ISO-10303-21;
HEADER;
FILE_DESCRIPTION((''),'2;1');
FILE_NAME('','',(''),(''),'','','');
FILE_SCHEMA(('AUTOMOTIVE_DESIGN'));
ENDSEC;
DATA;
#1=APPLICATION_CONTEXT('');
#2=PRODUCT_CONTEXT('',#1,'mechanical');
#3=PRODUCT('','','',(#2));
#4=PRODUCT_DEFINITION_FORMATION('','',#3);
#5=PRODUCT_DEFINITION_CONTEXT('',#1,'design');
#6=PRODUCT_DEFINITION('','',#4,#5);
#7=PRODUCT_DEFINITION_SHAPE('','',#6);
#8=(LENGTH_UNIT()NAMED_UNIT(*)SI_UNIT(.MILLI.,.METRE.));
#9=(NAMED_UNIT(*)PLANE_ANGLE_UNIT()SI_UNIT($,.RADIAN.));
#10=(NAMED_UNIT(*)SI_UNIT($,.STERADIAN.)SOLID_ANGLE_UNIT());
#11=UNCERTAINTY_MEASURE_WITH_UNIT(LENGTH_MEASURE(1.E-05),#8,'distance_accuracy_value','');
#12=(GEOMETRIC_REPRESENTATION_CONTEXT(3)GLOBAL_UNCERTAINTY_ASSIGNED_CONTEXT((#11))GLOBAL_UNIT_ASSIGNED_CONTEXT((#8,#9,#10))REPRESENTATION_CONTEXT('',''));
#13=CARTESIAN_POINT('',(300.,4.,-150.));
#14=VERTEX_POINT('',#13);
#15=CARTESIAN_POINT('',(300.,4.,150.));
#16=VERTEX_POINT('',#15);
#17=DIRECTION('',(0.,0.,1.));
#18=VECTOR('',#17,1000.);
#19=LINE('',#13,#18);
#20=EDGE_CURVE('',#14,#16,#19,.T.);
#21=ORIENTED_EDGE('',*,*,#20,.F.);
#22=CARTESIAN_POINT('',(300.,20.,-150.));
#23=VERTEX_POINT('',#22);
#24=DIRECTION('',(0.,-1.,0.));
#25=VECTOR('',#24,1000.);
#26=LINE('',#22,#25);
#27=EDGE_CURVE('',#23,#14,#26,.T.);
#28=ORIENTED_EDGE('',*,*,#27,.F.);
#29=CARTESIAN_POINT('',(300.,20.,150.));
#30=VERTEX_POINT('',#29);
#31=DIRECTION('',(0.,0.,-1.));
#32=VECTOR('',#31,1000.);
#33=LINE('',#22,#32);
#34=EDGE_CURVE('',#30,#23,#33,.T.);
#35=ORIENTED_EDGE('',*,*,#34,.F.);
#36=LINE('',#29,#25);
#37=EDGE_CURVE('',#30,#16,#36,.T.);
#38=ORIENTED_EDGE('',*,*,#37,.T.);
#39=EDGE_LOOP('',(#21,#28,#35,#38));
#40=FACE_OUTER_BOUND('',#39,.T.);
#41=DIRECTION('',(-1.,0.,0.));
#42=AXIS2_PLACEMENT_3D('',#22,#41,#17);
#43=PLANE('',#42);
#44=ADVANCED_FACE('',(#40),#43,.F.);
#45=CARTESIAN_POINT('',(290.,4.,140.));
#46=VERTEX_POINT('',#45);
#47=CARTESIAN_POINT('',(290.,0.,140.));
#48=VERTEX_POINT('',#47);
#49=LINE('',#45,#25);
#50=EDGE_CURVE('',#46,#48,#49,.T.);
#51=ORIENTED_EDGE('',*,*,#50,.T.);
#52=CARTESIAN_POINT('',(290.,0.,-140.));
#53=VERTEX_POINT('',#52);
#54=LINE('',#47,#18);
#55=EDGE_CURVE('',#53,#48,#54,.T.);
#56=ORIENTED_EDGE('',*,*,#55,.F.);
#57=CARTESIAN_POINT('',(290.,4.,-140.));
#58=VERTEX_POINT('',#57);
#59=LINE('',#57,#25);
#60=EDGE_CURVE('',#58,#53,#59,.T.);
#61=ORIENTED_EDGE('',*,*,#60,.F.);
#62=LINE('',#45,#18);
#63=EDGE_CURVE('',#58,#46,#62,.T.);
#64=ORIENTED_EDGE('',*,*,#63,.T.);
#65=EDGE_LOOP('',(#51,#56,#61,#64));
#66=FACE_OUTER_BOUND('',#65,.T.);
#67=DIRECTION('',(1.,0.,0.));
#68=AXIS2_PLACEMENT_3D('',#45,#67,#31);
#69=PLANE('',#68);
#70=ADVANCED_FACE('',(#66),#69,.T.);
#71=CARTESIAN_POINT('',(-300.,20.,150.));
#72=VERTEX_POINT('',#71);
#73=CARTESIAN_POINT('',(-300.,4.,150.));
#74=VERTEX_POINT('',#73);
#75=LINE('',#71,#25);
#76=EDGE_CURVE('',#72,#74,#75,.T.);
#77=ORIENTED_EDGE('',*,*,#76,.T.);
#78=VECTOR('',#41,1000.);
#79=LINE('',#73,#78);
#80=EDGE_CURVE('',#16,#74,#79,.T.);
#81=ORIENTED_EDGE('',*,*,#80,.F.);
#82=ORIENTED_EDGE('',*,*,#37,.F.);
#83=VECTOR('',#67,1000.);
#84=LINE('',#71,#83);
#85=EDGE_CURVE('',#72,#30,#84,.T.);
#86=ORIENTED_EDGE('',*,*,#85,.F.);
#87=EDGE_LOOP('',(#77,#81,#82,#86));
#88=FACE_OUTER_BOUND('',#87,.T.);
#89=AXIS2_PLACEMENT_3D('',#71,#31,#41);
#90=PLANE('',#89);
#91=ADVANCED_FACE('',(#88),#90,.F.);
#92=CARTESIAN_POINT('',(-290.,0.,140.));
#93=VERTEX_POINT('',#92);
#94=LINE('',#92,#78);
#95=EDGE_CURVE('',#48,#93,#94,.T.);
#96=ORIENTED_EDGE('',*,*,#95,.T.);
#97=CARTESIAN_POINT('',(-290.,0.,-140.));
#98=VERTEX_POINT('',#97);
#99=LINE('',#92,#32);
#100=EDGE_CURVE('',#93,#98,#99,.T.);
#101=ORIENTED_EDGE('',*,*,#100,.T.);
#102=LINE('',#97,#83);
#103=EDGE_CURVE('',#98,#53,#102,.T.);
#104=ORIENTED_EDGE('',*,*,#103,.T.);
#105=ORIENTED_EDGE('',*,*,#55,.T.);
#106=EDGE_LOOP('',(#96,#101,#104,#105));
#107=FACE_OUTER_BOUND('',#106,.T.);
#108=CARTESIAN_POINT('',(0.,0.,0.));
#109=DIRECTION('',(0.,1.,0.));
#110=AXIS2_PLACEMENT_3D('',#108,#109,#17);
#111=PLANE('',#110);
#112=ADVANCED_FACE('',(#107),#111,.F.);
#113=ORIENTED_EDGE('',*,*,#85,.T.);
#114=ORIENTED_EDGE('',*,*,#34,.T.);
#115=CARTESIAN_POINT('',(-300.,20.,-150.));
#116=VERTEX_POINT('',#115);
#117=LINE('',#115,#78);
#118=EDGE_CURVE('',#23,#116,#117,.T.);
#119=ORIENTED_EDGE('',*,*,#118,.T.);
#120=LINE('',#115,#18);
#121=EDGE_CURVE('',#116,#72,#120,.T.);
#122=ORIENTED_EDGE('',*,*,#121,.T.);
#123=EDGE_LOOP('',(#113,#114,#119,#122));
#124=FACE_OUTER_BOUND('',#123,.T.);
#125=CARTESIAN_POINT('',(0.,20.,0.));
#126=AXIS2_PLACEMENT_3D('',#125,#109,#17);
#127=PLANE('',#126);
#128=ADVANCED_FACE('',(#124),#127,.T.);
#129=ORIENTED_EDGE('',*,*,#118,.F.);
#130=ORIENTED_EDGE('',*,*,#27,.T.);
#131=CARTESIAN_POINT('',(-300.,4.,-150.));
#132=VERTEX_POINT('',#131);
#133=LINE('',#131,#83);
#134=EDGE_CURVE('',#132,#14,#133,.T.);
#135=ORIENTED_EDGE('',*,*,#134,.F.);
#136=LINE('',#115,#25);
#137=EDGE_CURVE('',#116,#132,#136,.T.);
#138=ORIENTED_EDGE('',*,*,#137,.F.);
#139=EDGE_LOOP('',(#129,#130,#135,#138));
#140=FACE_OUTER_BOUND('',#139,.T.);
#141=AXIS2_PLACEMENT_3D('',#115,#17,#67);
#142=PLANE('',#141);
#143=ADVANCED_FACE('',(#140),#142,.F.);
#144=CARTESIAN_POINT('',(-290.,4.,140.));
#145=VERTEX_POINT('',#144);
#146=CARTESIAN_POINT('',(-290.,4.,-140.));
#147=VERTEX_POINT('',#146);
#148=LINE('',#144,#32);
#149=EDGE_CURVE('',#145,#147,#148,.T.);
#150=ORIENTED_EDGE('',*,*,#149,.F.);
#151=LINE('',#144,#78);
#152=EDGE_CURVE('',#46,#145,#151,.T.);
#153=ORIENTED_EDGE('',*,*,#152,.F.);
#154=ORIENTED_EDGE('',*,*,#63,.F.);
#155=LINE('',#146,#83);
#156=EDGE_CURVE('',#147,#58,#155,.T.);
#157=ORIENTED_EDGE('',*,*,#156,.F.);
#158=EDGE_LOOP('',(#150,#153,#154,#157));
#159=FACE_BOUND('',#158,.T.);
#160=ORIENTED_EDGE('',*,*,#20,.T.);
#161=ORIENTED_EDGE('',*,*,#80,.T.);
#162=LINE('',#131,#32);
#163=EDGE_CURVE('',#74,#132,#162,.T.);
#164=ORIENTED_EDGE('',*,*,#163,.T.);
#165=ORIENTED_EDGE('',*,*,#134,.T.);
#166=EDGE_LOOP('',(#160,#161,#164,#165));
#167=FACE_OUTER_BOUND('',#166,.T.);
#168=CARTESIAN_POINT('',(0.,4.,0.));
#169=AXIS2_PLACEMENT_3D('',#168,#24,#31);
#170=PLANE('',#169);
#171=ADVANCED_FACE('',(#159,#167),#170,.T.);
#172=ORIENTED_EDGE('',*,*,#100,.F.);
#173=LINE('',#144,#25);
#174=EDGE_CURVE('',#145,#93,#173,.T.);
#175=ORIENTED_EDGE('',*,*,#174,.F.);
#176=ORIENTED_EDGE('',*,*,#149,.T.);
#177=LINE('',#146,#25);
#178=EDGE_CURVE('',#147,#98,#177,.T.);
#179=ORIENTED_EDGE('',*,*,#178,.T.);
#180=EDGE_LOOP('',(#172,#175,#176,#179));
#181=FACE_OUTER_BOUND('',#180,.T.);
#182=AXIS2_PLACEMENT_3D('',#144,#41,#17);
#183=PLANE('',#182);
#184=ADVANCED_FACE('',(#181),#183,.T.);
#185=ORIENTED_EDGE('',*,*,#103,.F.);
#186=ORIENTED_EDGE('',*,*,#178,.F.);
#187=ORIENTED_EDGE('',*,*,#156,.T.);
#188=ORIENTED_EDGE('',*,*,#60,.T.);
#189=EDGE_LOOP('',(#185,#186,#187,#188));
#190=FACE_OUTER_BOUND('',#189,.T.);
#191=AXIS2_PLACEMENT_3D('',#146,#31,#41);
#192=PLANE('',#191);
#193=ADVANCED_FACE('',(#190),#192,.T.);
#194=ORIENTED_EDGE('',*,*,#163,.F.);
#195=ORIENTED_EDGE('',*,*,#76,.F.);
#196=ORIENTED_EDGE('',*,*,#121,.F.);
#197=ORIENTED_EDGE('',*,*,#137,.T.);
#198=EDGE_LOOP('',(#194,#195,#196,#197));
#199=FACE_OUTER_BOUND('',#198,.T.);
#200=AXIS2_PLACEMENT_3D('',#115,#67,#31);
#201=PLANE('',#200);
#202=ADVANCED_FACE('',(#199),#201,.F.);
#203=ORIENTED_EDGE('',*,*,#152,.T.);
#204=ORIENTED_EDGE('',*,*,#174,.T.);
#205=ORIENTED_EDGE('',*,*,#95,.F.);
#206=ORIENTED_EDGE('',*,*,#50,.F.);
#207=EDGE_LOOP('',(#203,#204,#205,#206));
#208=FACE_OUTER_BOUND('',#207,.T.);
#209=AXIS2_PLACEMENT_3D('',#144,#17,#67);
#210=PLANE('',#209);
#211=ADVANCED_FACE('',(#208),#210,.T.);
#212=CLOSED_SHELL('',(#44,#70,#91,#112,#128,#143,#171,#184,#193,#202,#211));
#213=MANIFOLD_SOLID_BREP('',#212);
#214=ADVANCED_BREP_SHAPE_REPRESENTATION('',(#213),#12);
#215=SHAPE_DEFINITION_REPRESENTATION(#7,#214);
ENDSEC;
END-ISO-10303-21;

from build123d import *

# Parameters (mm, degrees)
SKETCH1_W           = 600
SKETCH1_H           = 300
BOSS_EXTRUDE1_DEPTH = 20
SKETCH2_OUTSIDE_W   = 736.224
SKETCH2_OUTSIDE_H   = 436.224
SKETCH2_OUTSIDE_W_2 = 580
SKETCH2_OUTSIDE_H_2 = 280
CUT_EXTRUDE1_DEPTH  = 4


with BuildPart() as part:
    # Sketch1 → Boss-Extrude1 (new body)
    with BuildSketch(Plane(origin=(0, 0, 0), x_dir=(1, 0, 0), z_dir=(0, 1, 0))):
        Rectangle(SKETCH1_W, SKETCH1_H)
    extrude(amount=BOSS_EXTRUDE1_DEPTH)

    # Sketch2 outside → Cut-Extrude1 (cut)
    with BuildSketch(Plane.XZ):
        Rectangle(SKETCH2_OUTSIDE_W, SKETCH2_OUTSIDE_H)
        Rectangle(SKETCH2_OUTSIDE_W_2, SKETCH2_OUTSIDE_H_2, mode=Mode.SUBTRACT)
    extrude(amount=-CUT_EXTRUDE1_DEPTH, mode=Mode.SUBTRACT)


solid = part.part
